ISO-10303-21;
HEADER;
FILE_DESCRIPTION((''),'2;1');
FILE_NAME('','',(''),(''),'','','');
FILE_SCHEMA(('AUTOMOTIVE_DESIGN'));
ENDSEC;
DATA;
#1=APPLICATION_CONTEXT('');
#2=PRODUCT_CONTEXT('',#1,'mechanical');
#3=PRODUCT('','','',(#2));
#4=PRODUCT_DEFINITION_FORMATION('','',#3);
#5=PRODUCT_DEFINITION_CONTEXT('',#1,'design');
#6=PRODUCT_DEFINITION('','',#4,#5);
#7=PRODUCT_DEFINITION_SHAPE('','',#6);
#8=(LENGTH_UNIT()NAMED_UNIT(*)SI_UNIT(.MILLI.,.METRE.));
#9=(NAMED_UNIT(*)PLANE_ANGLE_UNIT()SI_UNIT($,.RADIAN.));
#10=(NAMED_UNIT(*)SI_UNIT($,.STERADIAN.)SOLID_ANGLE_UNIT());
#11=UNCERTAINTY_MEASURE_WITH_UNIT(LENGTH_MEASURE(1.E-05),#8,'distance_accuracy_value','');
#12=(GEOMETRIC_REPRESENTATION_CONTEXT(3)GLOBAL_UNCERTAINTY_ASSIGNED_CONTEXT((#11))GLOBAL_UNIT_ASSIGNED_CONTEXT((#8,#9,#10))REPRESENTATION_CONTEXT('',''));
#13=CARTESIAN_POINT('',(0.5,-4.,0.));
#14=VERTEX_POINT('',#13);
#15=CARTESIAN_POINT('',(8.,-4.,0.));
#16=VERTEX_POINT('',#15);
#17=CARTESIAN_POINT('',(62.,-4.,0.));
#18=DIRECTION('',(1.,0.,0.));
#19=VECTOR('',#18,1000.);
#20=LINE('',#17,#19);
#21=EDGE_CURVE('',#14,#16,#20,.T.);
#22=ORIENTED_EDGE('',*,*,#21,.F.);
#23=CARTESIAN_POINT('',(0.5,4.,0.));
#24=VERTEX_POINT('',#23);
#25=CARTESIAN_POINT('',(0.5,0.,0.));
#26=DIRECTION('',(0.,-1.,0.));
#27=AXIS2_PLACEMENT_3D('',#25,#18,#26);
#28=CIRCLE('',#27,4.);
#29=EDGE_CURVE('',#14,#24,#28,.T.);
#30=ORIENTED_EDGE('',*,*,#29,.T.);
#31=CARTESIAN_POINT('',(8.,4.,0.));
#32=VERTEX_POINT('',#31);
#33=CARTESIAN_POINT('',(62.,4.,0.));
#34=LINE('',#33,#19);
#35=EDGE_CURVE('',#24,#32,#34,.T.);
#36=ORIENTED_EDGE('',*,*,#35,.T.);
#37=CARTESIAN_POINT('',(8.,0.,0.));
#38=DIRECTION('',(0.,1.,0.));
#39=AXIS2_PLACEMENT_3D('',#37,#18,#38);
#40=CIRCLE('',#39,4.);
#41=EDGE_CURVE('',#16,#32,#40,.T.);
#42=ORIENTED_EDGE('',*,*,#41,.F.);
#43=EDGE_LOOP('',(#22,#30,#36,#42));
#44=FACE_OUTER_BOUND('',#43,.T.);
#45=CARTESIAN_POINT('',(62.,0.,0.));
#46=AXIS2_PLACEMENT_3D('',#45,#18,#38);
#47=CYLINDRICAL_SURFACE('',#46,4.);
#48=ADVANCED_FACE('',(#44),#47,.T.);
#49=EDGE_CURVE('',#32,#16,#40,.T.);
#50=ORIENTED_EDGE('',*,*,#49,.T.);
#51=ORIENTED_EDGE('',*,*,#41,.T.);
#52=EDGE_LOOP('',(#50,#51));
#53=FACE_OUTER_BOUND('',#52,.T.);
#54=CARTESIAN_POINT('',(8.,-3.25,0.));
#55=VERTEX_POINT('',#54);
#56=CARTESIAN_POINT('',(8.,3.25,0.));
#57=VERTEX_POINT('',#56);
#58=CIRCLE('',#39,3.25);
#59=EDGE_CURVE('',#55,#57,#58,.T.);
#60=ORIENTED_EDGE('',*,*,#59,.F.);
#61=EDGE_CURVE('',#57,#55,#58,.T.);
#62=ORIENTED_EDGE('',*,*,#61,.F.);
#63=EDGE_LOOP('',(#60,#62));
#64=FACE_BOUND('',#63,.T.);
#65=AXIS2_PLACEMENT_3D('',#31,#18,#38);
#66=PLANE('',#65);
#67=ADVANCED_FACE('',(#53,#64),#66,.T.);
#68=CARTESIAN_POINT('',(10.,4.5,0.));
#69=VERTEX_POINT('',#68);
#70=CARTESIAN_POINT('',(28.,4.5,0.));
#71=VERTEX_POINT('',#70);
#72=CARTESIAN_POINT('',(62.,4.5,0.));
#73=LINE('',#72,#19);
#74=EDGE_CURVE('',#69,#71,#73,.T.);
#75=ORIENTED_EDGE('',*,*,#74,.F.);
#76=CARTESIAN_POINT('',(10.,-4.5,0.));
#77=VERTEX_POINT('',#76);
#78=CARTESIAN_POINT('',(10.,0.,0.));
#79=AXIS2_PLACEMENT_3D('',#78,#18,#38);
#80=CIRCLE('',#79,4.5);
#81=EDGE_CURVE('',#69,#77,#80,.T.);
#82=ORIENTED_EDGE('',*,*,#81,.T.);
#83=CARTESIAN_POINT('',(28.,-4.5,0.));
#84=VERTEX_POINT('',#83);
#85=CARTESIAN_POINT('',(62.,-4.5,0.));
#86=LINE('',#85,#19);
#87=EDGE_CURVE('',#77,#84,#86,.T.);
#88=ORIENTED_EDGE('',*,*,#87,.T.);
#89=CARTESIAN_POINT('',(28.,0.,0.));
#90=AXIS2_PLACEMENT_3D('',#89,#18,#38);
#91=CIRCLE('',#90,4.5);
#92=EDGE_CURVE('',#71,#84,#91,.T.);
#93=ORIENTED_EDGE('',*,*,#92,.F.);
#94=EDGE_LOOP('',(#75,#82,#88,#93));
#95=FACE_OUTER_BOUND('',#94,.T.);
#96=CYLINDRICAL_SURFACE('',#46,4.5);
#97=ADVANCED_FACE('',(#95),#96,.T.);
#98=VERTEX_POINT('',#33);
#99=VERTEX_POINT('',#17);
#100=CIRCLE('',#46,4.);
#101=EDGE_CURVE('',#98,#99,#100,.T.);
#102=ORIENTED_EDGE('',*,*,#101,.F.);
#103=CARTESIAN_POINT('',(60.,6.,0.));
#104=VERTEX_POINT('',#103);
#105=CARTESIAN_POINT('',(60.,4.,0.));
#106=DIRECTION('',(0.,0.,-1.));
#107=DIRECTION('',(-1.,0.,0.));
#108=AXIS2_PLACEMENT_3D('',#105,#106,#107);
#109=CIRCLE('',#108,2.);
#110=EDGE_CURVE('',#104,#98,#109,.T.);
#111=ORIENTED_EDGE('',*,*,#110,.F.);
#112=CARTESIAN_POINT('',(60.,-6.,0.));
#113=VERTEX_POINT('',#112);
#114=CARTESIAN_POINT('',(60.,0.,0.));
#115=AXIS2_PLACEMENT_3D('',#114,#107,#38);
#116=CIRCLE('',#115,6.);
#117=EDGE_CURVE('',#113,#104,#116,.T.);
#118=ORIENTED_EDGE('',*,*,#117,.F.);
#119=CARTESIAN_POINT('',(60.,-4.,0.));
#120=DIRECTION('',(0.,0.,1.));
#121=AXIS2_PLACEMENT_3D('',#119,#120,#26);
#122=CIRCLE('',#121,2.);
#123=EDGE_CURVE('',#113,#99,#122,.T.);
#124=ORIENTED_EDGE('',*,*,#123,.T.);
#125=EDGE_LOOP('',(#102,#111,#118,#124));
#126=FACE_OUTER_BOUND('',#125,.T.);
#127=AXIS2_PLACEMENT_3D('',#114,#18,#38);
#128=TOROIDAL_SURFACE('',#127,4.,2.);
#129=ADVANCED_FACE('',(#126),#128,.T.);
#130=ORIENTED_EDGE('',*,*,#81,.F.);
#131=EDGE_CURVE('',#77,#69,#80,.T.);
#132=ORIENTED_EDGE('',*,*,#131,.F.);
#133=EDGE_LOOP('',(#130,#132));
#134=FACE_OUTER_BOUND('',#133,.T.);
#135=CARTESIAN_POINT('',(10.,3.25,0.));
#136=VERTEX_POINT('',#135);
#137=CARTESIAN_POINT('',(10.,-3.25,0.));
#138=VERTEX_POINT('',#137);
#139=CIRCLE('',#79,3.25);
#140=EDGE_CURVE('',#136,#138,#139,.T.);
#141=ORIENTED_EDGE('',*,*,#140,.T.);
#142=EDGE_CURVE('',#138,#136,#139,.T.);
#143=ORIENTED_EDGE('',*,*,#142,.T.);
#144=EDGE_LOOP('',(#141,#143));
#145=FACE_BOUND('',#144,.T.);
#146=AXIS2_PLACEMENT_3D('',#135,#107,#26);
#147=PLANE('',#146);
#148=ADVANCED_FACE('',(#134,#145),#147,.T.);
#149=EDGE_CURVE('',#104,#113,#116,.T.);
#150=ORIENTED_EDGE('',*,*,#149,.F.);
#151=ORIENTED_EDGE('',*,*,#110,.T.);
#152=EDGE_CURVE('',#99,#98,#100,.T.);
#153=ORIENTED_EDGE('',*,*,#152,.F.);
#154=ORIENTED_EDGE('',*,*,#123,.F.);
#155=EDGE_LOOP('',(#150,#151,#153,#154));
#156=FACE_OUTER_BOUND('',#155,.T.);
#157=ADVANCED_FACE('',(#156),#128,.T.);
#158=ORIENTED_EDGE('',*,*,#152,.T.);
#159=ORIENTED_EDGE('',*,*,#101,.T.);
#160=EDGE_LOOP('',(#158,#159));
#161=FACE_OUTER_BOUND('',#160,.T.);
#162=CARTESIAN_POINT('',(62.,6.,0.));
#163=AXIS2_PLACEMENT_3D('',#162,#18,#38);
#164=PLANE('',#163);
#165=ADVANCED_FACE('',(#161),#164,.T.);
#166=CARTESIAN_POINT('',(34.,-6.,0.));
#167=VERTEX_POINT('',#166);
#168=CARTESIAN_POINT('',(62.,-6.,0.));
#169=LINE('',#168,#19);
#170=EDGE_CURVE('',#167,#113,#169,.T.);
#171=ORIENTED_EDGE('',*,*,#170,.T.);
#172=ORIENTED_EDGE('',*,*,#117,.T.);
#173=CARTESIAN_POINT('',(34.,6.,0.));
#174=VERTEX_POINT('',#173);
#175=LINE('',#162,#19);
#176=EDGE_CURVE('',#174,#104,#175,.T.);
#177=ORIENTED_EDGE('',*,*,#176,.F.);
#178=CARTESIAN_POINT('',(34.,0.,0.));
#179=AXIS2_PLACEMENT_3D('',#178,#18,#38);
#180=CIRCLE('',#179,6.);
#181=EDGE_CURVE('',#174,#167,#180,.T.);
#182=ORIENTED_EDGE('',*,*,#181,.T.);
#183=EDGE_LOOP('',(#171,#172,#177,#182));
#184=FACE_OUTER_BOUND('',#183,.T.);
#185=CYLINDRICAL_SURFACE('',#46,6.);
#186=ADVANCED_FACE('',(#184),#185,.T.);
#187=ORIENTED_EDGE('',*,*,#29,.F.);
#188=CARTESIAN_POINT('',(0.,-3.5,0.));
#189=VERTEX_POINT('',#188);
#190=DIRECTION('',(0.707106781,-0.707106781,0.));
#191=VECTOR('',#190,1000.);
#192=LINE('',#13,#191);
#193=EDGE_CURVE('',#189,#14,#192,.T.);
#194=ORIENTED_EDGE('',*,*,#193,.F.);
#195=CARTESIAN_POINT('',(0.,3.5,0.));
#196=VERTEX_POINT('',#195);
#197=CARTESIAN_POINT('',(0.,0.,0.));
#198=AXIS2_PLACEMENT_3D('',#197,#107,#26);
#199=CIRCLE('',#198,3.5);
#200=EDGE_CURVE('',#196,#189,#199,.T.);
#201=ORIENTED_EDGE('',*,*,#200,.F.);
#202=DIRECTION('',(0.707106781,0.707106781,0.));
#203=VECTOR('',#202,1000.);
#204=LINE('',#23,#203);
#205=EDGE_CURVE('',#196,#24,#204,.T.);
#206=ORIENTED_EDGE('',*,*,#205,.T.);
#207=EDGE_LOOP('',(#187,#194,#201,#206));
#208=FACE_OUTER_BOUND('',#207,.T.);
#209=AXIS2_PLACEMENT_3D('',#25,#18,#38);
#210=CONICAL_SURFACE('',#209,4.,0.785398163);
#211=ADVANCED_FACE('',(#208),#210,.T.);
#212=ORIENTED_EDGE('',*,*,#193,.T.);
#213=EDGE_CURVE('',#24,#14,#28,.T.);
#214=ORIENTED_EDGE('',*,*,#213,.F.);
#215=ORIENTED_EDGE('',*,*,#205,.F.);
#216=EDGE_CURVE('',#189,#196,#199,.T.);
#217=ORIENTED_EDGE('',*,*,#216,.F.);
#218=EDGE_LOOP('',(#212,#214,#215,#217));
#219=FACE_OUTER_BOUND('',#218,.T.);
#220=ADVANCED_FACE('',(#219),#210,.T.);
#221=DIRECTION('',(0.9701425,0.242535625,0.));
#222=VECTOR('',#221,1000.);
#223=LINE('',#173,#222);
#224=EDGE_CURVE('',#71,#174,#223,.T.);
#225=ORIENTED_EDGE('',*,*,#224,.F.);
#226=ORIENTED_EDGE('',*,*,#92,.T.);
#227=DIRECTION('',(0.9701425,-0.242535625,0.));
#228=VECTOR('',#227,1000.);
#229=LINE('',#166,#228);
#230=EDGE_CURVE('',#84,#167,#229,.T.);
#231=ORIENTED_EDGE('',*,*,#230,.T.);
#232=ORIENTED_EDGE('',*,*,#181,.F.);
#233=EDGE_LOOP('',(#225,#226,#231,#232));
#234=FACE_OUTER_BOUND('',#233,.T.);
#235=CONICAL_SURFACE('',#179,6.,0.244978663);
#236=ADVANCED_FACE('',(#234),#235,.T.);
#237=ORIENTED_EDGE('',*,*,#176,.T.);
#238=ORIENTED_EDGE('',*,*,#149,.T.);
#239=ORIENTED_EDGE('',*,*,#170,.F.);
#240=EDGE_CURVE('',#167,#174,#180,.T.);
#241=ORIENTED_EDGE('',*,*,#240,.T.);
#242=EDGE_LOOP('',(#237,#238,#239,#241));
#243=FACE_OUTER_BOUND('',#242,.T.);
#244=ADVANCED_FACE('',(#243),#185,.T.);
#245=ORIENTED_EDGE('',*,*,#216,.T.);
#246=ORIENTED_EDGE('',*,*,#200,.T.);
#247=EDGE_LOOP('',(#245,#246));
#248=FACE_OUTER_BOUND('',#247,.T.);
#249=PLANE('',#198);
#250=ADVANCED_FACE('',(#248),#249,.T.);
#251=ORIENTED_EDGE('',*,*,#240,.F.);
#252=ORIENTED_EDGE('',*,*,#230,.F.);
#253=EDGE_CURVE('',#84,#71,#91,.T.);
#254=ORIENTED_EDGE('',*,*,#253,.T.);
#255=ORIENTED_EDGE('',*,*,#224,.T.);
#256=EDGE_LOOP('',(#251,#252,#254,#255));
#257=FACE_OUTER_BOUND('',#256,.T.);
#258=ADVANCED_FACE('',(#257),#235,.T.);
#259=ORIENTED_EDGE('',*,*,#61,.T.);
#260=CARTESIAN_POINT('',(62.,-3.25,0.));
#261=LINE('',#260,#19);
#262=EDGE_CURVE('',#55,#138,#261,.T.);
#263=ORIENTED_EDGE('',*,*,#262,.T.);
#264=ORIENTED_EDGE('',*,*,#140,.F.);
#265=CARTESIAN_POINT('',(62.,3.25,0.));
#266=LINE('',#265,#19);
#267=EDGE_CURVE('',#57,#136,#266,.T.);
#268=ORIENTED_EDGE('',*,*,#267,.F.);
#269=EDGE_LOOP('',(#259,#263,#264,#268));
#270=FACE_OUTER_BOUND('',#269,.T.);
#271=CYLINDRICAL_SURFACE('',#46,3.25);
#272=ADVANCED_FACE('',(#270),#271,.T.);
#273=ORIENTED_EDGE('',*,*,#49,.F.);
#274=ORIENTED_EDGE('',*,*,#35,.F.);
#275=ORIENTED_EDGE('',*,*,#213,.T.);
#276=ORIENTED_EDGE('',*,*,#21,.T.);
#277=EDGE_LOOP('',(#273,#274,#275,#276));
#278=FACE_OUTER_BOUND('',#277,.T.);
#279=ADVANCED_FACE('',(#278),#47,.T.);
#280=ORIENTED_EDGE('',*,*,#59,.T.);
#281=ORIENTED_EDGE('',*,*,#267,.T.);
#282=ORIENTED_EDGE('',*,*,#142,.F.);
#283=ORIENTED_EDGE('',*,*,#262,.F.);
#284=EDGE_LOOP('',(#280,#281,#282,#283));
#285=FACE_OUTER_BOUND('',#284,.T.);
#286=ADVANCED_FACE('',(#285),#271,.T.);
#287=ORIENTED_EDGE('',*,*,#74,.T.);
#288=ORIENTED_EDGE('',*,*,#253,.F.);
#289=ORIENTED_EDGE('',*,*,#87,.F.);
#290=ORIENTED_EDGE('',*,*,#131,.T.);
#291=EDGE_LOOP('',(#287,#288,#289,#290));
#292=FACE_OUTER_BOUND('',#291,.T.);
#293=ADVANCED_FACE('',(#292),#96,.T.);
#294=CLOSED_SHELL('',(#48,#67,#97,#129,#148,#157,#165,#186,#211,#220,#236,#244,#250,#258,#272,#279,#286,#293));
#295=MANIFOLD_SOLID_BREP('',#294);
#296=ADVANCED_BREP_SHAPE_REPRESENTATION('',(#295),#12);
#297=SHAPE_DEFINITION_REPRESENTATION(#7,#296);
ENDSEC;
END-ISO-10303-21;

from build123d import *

# Parameters (mm, degrees)
FILLET1_R     = 2
CHAMFER1_SIZE = 0.5


with BuildPart() as part:
    # Sketch1 → Revolve1 (revolve)
    with BuildSketch(Plane.XY):
        Polygon((0, 0), (0, 4), (8, 4), (8, 3.25), (10, 3.25), (10, 4.5), (28, 4.5), (34, 6), (62, 6), (62, 0), align=None)
    revolve(axis=Axis((62, 0, 0), (-1, 0, 0)))

    # Fillet1
    fillet1_edges = [part.edges().sort_by_distance(p)[0] for p in [
        (62, -6, 0),
    ]]
    fillet(fillet1_edges, radius=FILLET1_R)

    # Chamfer1
    chamfer1_edges = [part.edges().sort_by_distance(p)[0] for p in [
        (0, -4, 0),
    ]]
    chamfer(chamfer1_edges, length=CHAMFER1_SIZE)


solid = part.part
